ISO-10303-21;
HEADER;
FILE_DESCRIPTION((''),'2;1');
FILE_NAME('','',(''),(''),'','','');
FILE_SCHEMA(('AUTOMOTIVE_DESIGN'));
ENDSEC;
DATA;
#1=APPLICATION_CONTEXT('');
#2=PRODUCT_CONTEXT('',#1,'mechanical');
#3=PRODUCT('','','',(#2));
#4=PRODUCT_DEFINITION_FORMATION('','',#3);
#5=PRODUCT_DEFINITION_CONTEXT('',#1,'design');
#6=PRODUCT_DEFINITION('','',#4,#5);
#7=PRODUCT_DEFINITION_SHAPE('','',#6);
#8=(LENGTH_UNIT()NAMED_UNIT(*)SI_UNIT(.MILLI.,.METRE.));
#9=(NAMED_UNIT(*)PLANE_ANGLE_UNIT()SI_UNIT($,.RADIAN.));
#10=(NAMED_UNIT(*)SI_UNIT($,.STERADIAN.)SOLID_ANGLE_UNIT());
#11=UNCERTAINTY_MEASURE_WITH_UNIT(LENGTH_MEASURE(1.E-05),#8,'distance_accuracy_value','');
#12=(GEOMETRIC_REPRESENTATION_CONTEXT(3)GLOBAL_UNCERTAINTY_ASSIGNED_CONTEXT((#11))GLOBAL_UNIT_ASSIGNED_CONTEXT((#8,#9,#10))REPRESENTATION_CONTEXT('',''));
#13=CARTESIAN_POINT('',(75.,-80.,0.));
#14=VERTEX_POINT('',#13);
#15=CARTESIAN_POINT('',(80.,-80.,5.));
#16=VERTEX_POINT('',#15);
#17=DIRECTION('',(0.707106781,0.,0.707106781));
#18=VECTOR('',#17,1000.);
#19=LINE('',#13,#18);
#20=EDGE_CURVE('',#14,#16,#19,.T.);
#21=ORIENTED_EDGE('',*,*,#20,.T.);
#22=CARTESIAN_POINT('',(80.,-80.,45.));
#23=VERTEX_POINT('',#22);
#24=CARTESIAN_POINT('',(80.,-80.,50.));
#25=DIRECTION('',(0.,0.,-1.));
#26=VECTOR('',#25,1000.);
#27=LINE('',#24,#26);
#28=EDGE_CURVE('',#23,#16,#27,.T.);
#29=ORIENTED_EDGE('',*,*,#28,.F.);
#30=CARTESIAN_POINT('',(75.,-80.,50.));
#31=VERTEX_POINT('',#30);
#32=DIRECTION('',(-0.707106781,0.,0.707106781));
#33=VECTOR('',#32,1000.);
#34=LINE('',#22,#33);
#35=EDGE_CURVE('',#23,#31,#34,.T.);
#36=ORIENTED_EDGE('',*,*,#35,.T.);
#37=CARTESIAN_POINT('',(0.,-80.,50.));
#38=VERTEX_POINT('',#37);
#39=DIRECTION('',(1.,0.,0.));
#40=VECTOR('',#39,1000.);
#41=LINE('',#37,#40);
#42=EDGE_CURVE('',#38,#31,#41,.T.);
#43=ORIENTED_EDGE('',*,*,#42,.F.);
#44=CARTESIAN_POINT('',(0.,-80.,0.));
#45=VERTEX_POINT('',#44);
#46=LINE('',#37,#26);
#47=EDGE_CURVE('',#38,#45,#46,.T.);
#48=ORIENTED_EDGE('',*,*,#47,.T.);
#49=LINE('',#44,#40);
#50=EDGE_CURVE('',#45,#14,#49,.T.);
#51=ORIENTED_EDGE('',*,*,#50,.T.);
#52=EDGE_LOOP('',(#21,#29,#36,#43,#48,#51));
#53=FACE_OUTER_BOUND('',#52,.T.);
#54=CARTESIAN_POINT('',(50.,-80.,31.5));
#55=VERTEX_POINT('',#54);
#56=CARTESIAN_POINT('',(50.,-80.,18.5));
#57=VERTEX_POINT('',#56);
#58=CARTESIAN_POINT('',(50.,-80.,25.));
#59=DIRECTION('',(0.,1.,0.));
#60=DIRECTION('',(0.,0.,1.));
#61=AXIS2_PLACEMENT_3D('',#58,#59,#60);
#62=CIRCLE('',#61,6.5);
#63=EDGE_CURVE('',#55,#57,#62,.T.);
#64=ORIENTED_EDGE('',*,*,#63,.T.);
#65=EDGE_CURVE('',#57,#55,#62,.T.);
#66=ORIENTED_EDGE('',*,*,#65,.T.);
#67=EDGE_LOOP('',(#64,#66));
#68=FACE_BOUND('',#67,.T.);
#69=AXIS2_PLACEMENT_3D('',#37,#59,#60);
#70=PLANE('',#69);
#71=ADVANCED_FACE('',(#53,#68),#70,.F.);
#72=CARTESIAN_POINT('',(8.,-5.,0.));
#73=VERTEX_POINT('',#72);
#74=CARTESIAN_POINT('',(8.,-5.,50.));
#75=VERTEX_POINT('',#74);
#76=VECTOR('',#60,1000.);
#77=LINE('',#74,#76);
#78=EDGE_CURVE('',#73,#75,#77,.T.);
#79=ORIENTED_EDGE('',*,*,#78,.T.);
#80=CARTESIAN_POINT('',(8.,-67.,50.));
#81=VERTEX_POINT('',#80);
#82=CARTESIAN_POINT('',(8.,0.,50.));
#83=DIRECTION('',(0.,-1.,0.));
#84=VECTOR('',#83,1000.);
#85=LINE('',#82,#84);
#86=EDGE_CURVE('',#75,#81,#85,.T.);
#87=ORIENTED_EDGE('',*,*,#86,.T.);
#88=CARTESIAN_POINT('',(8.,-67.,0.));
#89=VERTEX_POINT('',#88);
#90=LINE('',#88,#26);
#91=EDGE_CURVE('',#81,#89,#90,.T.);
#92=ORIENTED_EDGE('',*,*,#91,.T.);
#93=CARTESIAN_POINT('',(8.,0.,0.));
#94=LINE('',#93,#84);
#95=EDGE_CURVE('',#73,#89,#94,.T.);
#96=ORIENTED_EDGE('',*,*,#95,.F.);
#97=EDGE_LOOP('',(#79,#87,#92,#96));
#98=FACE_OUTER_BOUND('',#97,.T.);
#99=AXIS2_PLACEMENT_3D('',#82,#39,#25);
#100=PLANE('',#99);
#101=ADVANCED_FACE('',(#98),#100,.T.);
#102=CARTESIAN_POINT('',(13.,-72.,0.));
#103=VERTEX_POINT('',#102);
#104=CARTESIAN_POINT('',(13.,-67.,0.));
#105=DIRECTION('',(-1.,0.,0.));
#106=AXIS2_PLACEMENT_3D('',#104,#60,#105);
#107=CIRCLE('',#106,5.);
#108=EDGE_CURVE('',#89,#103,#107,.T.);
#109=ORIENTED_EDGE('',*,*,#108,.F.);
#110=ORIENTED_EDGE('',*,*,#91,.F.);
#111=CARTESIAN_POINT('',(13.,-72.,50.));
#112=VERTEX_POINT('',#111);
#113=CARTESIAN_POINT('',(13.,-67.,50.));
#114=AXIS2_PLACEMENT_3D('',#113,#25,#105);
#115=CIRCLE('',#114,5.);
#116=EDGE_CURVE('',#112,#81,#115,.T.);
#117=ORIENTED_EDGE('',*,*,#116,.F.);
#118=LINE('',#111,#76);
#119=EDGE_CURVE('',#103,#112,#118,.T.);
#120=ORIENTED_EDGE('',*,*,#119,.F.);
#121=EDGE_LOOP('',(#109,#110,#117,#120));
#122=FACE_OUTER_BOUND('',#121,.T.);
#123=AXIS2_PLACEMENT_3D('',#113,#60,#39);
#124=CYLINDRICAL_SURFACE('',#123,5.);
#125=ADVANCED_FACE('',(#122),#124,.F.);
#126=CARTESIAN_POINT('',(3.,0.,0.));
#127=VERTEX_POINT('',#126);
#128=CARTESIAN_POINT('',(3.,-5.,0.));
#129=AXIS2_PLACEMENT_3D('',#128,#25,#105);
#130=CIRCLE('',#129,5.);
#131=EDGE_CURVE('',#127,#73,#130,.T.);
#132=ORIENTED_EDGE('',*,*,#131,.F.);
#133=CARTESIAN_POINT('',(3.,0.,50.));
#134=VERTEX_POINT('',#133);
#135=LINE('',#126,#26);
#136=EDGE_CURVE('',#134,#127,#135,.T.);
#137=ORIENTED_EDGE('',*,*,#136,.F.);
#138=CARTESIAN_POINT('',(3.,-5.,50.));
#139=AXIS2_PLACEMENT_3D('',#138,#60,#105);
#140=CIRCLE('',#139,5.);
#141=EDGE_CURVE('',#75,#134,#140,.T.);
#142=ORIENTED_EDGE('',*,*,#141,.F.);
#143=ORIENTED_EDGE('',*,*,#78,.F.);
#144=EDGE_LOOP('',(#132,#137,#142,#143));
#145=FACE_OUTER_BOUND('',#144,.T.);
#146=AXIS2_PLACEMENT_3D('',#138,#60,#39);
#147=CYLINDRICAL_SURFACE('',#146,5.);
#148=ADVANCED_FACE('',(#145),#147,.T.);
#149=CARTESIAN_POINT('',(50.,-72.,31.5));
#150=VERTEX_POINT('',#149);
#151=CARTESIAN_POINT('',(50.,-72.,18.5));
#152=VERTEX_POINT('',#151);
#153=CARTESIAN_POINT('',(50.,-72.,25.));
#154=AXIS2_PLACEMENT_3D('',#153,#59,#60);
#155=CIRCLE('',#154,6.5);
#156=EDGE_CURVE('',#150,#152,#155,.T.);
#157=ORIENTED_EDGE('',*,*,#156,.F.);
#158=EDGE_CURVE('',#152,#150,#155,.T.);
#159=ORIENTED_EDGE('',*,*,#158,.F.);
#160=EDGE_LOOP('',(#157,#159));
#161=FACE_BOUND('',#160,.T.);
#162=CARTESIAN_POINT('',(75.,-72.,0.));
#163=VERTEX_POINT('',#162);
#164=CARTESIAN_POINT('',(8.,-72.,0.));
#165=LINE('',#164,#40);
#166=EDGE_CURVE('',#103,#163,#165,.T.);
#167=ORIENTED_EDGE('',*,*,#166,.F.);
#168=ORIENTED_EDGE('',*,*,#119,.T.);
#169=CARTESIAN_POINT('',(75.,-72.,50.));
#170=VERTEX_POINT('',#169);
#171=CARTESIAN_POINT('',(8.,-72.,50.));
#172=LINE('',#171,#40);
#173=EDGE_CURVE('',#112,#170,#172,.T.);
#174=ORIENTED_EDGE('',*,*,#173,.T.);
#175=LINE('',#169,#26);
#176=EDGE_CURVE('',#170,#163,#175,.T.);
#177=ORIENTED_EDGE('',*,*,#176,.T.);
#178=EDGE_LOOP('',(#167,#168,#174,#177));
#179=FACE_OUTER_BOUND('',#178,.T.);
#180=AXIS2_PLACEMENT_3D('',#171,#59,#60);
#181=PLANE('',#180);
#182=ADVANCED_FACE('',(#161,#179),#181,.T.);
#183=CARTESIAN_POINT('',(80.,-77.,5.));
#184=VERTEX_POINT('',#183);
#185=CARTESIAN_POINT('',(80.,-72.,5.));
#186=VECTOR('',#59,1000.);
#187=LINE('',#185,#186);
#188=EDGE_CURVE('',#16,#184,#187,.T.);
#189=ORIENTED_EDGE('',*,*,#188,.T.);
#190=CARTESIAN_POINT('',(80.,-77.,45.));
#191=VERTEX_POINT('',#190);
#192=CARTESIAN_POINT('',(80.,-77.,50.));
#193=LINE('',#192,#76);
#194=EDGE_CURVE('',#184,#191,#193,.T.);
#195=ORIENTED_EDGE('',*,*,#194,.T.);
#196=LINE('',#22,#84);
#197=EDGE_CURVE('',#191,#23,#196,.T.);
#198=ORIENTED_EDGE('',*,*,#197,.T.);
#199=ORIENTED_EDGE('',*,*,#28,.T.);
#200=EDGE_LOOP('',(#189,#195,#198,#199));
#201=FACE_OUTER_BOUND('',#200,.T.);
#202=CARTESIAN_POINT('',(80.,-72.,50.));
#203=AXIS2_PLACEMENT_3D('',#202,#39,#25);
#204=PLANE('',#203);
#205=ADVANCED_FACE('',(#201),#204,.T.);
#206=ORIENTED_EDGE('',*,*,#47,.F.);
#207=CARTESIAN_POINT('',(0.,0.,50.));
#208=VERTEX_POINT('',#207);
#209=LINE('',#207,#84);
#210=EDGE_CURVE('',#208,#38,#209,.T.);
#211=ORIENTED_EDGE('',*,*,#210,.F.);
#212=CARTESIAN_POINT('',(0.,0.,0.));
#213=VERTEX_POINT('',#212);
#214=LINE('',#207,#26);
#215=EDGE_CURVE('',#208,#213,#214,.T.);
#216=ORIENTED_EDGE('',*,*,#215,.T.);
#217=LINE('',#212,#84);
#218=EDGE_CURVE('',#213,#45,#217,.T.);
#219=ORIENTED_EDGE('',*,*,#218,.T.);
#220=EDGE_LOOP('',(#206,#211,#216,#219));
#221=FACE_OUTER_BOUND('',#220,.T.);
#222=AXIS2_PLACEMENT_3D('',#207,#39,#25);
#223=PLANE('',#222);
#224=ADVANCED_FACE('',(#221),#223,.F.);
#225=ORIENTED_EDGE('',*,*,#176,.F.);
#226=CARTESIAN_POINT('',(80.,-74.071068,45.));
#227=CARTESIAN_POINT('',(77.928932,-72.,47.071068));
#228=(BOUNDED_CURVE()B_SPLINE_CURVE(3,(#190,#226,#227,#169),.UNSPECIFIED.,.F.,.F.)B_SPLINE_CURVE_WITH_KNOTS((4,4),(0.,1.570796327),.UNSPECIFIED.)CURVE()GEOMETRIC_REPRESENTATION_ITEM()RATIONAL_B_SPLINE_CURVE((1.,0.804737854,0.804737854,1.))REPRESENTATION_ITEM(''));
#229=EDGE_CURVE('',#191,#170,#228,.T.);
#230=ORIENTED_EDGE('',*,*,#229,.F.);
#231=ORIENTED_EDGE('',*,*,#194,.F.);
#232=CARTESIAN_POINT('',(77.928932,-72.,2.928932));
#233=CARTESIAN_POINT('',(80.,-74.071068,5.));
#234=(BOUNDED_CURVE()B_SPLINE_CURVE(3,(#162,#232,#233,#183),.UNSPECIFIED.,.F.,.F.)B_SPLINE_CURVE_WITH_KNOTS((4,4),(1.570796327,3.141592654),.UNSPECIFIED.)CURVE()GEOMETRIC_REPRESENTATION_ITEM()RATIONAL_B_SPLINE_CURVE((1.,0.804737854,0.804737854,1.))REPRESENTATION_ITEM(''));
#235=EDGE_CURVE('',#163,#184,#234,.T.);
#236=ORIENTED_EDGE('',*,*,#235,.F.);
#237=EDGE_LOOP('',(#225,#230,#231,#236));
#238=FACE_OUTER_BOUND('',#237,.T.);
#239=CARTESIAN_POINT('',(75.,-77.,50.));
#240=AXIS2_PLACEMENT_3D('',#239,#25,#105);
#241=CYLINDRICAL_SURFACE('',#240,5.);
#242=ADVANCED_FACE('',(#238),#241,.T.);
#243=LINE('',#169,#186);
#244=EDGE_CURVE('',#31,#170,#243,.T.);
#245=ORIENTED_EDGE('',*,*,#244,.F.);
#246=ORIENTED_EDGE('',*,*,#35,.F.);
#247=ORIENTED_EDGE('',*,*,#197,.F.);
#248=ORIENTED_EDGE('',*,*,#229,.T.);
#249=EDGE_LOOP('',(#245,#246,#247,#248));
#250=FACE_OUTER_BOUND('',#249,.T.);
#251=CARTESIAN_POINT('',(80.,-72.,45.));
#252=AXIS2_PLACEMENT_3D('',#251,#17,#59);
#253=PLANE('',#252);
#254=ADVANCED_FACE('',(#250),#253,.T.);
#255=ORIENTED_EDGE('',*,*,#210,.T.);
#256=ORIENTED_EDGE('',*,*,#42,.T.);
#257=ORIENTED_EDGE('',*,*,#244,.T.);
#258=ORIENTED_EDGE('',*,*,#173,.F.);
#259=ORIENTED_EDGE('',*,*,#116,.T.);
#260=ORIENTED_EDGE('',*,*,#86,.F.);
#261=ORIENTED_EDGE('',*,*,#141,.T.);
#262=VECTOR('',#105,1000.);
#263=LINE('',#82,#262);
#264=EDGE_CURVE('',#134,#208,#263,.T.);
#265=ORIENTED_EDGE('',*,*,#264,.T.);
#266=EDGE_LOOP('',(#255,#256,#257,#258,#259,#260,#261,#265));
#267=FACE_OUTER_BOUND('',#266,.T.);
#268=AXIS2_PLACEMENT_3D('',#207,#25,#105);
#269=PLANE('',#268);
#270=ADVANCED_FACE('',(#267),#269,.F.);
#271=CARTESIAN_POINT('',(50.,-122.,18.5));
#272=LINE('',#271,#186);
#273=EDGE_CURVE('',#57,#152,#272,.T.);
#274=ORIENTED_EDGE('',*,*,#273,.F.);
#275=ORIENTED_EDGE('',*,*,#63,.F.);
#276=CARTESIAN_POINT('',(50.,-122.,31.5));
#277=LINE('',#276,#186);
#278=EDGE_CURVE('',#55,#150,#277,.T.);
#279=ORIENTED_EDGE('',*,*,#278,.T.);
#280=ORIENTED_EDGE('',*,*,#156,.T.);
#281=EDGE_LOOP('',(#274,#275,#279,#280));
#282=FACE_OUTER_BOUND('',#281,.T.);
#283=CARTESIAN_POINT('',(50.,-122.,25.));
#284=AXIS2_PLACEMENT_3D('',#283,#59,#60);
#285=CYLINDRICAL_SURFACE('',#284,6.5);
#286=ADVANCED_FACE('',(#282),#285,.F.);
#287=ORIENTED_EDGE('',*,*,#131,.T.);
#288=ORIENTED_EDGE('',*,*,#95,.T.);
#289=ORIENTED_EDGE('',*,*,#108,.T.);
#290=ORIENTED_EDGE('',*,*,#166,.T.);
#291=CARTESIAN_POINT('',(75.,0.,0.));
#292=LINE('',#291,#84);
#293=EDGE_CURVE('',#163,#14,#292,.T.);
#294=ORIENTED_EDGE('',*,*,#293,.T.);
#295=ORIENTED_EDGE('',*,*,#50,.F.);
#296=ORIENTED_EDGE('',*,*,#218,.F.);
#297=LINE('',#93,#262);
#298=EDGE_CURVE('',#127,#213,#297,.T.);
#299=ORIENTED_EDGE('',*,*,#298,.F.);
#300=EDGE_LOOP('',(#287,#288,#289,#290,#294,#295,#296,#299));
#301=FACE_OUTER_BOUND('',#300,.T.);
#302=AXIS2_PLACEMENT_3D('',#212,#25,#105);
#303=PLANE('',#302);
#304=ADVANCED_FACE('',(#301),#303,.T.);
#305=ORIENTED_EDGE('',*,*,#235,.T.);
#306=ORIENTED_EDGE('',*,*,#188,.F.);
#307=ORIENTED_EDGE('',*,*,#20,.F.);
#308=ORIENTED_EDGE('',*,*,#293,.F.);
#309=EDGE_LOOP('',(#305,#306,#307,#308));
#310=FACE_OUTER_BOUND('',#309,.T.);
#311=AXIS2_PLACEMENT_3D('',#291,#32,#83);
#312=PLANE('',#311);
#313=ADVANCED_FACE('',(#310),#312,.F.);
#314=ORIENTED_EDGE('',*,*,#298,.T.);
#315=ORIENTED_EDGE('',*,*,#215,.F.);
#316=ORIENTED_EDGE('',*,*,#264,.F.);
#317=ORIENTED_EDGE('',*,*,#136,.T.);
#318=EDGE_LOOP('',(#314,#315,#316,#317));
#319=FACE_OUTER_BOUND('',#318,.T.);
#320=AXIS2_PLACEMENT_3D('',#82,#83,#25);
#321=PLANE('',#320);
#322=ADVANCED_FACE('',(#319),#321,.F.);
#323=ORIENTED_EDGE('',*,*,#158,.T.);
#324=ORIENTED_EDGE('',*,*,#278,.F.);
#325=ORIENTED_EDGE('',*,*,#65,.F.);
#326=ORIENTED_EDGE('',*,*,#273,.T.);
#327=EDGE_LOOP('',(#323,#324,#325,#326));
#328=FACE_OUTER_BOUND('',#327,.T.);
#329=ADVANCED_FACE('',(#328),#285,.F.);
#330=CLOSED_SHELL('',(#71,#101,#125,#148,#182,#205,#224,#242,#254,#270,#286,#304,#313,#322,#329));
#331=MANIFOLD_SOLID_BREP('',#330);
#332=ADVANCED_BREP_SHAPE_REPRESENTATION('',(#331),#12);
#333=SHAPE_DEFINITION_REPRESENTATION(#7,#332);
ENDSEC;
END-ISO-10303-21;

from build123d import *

# Parameters (mm, degrees)
EXTRUDE_1_DEPTH     = 50
SKETCH_2_R          = 6.5
CUT_EXTRUDE_1_DEPTH = 50
FILLET_1_R          = 5
FILLET_2_R          = 5
CHAMFER_1_SIZE      = 5
FILLET_3_R          = 5


with BuildPart() as part:
    # 草图1 → 凸台-拉伸1 (new body)
    with BuildSketch(Plane.XY):
        Polygon((0, 0), (0, -80), (80, -80), (80, -72), (8, -72), (8, 0), align=None)
    extrude(amount=EXTRUDE_1_DEPTH)

    # 草图2 → 切除-拉伸1 (cut)
    with BuildSketch(Plane(origin=(0, -72, 0), x_dir=(1, 0, 0), z_dir=(0, 1, 0))):
        with Locations(Location((50, -25, 0), (0, 0, 270))):
            Circle(SKETCH_2_R)
    extrude(amount=-CUT_EXTRUDE_1_DEPTH, mode=Mode.SUBTRACT)

    # 圆角1
    fillet_1_edges = [part.edges().sort_by_distance(p)[0] for p in [
        (8, -72, 25),
    ]]
    fillet(fillet_1_edges, radius=FILLET_1_R)

    # 圆角2
    fillet_2_edges = [part.edges().sort_by_distance(p)[0] for p in [
        (8, 0, 25),
    ]]
    fillet(fillet_2_edges, radius=FILLET_2_R)

    # 倒角1
    chamfer_1_edges = [part.edges().sort_by_distance(p)[0] for p in [
        (80, -76, 0),
        (80, -76, 50),
    ]]
    chamfer(chamfer_1_edges, length=CHAMFER_1_SIZE)

    # 圆角3
    fillet_3_edges = [part.edges().sort_by_distance(p)[0] for p in [
        (80, -72, 25),
    ]]
    fillet(fillet_3_edges, radius=FILLET_3_R)


solid = part.part
